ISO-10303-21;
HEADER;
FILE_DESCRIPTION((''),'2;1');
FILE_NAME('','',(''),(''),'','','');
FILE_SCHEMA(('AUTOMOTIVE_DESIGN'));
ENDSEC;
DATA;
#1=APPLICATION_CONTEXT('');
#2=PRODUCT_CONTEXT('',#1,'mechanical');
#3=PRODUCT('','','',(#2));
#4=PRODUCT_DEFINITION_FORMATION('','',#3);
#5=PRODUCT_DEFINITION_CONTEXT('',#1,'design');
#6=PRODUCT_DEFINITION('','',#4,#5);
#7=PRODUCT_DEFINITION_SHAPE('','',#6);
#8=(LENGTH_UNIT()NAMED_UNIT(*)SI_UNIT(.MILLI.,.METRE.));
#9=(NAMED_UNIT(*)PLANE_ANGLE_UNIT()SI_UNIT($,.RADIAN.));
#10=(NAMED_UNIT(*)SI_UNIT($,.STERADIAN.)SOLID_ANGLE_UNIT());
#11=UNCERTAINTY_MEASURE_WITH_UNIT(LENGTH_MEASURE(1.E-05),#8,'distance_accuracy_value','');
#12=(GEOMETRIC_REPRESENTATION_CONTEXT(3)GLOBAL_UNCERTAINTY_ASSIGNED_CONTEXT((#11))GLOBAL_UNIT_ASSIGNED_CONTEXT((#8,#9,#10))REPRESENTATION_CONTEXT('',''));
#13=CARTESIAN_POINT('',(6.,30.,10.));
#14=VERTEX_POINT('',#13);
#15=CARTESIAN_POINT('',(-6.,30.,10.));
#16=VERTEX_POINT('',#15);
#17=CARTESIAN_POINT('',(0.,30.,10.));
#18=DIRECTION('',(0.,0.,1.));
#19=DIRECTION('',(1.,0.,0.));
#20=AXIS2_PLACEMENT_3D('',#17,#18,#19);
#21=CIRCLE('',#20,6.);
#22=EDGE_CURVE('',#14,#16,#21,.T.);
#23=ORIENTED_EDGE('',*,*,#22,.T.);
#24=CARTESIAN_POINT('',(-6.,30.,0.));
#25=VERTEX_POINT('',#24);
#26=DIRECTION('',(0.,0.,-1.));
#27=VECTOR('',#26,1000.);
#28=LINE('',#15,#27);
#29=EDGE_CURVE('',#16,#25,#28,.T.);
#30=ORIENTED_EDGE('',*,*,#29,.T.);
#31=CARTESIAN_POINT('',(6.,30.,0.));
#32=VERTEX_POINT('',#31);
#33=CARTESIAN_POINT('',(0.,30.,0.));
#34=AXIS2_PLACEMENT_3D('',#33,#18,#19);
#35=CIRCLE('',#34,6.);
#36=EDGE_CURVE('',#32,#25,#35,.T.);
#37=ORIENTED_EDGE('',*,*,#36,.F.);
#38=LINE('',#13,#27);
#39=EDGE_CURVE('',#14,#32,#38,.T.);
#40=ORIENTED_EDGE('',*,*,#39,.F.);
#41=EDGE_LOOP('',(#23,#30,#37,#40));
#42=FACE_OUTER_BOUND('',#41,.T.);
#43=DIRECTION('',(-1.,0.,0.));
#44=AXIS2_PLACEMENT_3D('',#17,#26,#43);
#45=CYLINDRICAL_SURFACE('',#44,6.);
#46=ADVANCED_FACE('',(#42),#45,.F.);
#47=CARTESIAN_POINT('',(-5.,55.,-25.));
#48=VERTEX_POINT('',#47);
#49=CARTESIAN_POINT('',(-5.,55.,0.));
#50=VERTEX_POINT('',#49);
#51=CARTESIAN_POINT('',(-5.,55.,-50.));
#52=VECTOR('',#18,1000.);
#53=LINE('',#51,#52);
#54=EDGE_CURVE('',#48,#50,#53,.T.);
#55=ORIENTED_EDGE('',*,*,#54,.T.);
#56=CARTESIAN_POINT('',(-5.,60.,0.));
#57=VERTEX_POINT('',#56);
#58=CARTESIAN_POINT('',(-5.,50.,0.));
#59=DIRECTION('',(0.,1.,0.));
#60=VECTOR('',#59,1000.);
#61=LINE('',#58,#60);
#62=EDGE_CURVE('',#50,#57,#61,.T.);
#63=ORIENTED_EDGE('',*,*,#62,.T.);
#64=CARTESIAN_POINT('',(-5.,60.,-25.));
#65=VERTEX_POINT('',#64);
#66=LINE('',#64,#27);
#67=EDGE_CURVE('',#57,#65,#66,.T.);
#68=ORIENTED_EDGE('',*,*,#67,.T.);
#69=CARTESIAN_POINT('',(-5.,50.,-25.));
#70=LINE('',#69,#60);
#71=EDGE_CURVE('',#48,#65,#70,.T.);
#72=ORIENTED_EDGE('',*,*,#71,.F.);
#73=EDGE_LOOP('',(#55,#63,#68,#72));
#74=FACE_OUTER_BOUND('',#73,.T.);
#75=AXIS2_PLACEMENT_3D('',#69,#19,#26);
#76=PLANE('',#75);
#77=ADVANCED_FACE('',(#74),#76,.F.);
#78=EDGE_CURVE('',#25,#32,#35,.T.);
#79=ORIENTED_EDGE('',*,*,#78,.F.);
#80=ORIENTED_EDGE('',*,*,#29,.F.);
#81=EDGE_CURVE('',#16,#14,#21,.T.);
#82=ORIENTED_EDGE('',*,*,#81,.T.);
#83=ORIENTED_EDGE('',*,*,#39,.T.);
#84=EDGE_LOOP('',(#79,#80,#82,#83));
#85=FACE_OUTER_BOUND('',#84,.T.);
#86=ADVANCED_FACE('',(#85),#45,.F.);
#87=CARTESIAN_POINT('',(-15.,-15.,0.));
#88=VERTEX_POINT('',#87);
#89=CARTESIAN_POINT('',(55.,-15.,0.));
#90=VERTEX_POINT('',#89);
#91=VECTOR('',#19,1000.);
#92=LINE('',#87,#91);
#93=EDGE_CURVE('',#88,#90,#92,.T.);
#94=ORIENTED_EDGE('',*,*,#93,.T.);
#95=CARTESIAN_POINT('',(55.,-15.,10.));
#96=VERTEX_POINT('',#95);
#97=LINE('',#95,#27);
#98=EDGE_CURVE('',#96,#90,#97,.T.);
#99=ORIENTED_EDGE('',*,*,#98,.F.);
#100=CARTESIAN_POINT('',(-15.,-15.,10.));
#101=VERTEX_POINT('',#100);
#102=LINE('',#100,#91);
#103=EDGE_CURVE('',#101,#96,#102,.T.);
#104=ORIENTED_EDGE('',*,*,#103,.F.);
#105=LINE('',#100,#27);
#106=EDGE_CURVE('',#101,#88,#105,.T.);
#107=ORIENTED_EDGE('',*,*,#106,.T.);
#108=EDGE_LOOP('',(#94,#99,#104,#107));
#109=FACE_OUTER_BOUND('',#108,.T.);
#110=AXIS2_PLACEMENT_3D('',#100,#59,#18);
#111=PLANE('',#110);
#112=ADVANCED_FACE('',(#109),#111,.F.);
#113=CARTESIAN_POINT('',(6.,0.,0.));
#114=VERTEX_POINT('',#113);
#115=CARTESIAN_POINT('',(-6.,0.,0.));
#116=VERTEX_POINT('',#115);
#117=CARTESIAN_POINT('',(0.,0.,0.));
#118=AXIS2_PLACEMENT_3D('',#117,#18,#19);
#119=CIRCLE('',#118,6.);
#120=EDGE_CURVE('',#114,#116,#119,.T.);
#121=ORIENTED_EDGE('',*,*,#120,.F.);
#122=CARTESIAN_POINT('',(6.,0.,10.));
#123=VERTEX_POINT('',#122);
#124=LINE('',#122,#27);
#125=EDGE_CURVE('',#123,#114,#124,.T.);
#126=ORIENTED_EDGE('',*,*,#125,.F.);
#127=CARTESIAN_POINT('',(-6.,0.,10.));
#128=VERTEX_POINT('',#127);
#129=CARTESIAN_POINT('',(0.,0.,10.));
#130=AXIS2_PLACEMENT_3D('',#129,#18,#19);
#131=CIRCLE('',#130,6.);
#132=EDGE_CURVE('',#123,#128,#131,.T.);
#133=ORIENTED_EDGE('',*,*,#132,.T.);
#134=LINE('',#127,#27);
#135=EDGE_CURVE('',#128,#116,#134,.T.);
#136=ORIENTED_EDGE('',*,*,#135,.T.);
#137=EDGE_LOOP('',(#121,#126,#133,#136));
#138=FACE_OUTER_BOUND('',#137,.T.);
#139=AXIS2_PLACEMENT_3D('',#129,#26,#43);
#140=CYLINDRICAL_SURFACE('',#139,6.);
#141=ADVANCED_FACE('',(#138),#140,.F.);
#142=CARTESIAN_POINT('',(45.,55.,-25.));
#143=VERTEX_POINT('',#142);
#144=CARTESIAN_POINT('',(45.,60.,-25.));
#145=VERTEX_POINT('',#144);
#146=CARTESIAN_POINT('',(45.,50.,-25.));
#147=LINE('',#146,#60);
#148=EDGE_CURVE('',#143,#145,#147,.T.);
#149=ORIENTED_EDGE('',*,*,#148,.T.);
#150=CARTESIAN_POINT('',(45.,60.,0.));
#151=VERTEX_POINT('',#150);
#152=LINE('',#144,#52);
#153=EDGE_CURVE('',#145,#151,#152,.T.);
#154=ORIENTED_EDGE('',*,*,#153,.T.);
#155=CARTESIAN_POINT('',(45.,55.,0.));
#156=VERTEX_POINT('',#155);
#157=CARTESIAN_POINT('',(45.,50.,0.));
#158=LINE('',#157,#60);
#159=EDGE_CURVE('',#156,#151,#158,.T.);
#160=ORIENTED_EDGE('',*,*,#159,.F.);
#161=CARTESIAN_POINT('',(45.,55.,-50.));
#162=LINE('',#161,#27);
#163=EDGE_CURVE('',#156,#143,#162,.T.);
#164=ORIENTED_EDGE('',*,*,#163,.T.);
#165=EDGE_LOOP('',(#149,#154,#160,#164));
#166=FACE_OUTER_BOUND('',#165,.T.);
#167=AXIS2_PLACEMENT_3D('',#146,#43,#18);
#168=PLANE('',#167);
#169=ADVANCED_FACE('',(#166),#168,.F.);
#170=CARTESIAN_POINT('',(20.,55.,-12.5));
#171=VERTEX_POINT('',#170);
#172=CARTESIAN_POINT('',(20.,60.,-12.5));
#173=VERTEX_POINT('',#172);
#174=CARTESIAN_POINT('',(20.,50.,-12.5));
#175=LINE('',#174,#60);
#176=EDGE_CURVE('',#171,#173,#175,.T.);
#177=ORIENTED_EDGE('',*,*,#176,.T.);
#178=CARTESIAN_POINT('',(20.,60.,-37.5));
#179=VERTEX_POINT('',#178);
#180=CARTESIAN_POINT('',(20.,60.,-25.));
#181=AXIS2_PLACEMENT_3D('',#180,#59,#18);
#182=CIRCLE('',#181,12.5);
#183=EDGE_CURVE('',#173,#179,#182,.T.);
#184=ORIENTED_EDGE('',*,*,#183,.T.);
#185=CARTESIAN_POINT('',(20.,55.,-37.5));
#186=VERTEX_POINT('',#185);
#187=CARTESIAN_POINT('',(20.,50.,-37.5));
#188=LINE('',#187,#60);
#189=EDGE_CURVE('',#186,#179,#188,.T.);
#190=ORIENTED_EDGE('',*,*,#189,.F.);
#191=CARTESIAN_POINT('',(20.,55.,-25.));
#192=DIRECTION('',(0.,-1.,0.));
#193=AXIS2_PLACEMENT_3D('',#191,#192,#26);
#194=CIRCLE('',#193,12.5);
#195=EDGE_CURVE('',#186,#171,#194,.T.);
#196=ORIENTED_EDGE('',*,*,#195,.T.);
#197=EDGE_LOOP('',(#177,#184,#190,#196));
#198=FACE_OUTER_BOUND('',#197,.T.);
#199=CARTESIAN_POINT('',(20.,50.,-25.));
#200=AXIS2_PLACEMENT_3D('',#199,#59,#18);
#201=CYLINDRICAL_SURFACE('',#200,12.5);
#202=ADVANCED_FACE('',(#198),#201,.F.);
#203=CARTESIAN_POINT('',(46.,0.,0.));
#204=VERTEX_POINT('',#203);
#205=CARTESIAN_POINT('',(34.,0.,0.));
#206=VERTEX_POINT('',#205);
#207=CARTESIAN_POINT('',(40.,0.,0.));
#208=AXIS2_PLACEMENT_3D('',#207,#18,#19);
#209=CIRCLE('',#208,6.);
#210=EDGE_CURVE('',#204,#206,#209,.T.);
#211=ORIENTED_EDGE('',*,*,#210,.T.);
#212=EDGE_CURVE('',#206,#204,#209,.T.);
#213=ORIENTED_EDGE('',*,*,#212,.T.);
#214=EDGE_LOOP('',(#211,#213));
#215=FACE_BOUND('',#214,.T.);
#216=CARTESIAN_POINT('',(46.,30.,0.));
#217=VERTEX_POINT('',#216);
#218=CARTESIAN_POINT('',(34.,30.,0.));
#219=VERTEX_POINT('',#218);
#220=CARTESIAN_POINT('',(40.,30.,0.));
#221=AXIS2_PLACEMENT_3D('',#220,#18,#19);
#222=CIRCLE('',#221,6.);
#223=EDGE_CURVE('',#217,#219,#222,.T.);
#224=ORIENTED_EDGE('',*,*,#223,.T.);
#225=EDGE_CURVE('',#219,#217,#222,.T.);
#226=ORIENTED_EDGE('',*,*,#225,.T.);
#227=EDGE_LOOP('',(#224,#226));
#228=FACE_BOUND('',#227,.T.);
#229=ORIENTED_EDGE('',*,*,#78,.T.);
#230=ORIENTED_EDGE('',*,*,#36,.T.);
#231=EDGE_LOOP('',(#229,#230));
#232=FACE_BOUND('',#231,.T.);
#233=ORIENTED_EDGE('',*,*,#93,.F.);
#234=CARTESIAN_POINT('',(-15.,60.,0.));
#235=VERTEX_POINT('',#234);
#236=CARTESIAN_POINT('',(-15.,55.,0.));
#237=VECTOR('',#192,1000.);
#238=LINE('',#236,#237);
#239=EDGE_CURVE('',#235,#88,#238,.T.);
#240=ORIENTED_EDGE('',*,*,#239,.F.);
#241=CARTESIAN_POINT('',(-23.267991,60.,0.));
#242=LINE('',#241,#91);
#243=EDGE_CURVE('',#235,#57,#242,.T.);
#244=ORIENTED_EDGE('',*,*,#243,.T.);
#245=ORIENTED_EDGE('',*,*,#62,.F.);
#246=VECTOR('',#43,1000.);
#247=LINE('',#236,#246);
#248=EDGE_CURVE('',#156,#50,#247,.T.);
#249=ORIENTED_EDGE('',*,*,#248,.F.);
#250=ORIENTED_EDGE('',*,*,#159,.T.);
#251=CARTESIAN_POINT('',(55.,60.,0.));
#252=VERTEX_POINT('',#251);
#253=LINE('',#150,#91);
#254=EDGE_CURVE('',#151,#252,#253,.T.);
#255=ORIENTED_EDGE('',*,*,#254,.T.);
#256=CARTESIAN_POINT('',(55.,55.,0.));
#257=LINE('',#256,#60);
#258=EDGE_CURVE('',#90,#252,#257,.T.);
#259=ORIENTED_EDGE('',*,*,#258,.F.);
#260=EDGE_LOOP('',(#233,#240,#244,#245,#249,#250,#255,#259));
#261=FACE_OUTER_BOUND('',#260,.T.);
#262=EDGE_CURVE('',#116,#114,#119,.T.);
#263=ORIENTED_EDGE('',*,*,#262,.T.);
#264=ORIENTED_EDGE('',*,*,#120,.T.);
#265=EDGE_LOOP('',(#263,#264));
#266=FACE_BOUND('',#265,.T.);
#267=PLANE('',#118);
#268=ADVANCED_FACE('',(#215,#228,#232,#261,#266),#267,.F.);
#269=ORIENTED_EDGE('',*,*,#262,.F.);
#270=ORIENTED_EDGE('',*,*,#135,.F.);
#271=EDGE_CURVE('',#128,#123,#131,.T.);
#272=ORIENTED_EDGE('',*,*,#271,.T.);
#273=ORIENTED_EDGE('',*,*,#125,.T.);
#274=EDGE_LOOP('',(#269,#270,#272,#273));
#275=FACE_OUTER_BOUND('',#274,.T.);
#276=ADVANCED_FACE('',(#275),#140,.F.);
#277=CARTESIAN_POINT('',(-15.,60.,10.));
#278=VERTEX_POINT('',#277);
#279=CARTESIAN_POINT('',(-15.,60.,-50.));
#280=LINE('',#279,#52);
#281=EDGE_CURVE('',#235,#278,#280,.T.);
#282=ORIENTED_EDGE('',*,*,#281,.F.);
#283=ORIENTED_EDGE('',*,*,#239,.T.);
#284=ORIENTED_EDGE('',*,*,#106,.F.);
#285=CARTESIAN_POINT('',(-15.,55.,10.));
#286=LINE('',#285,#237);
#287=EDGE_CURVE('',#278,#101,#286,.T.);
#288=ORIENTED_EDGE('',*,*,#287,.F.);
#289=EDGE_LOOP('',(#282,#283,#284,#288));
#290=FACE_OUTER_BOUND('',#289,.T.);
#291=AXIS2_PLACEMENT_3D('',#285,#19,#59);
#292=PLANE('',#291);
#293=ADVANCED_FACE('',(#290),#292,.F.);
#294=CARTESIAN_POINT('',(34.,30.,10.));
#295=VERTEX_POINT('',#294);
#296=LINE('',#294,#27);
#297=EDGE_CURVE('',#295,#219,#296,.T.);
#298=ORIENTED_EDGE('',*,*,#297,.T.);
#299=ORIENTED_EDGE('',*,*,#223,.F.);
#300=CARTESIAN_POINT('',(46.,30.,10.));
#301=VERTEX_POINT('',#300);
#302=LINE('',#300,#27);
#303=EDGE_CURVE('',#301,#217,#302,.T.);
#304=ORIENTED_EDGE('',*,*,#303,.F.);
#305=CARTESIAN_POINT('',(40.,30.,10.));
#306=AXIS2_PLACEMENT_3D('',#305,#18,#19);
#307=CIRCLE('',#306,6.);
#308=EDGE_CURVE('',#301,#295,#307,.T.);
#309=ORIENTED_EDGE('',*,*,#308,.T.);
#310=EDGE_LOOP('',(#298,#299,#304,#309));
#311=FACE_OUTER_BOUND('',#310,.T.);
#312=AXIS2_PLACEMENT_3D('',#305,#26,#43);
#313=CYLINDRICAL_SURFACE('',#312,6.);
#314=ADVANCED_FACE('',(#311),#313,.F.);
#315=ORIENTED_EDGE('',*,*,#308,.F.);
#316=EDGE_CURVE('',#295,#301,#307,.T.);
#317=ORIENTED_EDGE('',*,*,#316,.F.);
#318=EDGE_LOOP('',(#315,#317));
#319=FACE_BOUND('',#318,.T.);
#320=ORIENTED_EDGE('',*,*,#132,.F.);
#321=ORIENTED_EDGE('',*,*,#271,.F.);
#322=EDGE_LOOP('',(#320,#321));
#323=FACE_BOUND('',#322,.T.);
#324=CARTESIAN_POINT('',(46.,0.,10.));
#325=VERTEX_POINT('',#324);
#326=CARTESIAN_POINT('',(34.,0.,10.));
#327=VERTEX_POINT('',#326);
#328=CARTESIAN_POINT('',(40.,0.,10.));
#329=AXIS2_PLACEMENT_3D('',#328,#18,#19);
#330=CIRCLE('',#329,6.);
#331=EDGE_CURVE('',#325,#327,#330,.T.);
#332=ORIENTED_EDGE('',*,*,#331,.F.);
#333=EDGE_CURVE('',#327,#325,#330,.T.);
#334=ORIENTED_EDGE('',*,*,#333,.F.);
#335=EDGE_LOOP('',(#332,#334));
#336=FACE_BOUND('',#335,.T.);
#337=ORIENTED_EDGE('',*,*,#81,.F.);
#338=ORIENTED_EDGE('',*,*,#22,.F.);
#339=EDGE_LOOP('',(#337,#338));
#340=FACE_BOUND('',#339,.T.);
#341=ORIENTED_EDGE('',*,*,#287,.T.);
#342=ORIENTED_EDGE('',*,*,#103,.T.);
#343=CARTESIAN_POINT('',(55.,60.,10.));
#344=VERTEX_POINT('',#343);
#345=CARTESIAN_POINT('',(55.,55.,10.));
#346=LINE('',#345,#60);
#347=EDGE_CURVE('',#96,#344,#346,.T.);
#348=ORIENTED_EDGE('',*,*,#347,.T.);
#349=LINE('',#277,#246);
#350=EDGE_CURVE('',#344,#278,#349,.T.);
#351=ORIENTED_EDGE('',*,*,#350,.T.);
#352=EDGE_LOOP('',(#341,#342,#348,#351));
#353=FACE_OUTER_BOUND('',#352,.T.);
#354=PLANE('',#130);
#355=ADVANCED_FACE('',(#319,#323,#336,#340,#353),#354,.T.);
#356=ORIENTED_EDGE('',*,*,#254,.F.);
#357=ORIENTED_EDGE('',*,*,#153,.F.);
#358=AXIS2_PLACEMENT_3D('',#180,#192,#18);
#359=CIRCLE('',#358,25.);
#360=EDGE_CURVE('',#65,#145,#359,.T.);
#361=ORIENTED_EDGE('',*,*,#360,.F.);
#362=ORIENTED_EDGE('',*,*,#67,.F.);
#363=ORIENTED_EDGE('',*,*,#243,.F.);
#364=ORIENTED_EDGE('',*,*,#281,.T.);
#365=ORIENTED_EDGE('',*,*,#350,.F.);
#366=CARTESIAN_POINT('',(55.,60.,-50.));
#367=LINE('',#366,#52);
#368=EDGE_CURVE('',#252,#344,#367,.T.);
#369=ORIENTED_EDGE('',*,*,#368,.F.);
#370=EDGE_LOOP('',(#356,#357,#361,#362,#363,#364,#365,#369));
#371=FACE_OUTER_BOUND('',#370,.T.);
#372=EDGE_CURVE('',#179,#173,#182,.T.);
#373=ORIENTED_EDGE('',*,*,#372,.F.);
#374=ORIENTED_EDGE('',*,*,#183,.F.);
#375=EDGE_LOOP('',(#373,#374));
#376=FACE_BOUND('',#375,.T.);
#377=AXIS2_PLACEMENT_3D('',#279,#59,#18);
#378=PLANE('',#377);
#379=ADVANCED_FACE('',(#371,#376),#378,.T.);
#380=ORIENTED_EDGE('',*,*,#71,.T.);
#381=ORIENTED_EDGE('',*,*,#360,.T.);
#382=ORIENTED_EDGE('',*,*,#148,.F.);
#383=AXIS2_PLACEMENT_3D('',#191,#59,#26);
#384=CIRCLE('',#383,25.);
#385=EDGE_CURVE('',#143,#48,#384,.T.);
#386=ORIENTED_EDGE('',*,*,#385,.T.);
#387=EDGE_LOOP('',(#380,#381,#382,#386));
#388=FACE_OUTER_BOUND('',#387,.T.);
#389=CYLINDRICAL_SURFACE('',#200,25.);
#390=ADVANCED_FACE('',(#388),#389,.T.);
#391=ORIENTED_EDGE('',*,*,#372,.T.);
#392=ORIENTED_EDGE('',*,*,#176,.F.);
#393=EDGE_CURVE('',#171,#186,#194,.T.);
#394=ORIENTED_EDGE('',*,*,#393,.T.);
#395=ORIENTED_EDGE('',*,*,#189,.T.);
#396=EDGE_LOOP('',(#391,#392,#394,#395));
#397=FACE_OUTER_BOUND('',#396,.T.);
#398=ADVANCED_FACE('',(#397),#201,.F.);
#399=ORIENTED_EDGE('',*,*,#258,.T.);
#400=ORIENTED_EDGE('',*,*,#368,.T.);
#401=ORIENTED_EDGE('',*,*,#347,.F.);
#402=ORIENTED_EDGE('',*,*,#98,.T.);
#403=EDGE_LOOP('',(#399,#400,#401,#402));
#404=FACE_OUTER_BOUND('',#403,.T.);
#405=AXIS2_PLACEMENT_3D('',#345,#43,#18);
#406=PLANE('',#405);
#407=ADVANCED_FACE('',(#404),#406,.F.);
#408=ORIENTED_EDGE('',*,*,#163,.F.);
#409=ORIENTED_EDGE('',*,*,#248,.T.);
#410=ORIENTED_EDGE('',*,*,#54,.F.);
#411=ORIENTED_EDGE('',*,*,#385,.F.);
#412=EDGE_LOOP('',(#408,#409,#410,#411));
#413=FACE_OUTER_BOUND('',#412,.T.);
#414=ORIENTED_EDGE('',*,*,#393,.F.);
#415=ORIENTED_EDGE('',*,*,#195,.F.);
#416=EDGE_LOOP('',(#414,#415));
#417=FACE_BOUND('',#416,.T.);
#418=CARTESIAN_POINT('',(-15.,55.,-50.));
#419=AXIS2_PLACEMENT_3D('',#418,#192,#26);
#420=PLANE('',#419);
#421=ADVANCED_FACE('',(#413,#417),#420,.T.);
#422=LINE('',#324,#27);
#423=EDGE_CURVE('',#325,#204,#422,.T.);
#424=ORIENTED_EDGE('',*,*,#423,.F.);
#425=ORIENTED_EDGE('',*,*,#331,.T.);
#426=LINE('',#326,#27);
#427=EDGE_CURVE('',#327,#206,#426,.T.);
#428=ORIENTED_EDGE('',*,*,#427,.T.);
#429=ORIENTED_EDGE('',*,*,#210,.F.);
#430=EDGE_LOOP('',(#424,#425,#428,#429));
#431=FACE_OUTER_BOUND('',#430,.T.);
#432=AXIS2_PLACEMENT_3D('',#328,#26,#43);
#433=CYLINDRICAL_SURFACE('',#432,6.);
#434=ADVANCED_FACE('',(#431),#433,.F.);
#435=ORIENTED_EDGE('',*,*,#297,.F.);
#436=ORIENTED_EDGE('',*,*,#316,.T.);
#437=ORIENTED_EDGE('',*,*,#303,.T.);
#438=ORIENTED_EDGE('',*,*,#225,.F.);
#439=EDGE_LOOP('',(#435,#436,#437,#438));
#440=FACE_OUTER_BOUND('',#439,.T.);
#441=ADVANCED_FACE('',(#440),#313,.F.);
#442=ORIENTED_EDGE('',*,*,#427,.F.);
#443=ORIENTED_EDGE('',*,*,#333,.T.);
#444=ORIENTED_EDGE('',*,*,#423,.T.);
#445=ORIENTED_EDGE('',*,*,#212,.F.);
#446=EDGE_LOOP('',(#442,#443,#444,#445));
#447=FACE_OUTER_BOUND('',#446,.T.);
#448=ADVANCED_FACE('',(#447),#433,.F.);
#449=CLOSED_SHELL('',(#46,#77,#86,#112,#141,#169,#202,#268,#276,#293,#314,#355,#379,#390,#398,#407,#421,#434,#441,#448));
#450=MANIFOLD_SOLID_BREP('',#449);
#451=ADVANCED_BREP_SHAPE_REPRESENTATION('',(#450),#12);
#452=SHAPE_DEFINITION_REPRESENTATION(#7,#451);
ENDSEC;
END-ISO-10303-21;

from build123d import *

# Parameters (mm, degrees)
SKETCH_1_W          = 70
SKETCH_1_H          = 70
SKETCH_1_R          = 6
EXTRUDE_1_DEPTH     = 10
SKETCH_2_W          = 70
SKETCH_2_H          = 5
EXTRUDE_2_DEPTH     = 60
SKETCH_4_R          = 12.5
CUT_EXTRUDE_1_DEPTH = 10


with BuildPart() as part:
    # 草图1 → 凸台-拉伸1 (new body)
    with BuildSketch(Plane.XY):
        with Locations((20, 20)):
            Rectangle(SKETCH_1_W, SKETCH_1_H)
        Circle(SKETCH_1_R, mode=Mode.SUBTRACT)
        with Locations((0, 30)):
            Circle(SKETCH_1_R, mode=Mode.SUBTRACT)
        with Locations((40, 30)):
            Circle(SKETCH_1_R, mode=Mode.SUBTRACT)
        with Locations((40, 0)):
            Circle(SKETCH_1_R, mode=Mode.SUBTRACT)
    extrude(amount=EXTRUDE_1_DEPTH)

    # 草图2 → 凸台-拉伸2 (add)
    with BuildSketch(Plane.XY.offset(10)):
        with Locations((20, 57.5)):
            Rectangle(SKETCH_2_W, SKETCH_2_H)
    extrude(amount=-EXTRUDE_2_DEPTH)

    # 草图4 → 切除-拉伸1 (cut)
    with BuildSketch(Plane(origin=(0, 60, 0), x_dir=(1, 0, 0), z_dir=(0, 1, 0))):
        with Locations(Location((20, 25, 0), (0, 0, 270))):
            Circle(SKETCH_4_R)
        with BuildLine():
            Line((-5, 25), (-5, 0))
            Line((-5, 0), (-23.267990544, 0))
            Line((-23.267990544, 0), (-23.267990544, 53.705684911))
            Line((-23.267990544, 53.705684911), (55, 53.705684911))
            Line((55, 53.705684911), (55, 0))
            Line((55, 0), (45, 0))
            Line((45, 0), (45, 25))
            ThreePointArc((45, 25), (20, 50), (-5, 25))
        make_face()
    extrude(amount=-CUT_EXTRUDE_1_DEPTH, mode=Mode.SUBTRACT)


solid = part.part
